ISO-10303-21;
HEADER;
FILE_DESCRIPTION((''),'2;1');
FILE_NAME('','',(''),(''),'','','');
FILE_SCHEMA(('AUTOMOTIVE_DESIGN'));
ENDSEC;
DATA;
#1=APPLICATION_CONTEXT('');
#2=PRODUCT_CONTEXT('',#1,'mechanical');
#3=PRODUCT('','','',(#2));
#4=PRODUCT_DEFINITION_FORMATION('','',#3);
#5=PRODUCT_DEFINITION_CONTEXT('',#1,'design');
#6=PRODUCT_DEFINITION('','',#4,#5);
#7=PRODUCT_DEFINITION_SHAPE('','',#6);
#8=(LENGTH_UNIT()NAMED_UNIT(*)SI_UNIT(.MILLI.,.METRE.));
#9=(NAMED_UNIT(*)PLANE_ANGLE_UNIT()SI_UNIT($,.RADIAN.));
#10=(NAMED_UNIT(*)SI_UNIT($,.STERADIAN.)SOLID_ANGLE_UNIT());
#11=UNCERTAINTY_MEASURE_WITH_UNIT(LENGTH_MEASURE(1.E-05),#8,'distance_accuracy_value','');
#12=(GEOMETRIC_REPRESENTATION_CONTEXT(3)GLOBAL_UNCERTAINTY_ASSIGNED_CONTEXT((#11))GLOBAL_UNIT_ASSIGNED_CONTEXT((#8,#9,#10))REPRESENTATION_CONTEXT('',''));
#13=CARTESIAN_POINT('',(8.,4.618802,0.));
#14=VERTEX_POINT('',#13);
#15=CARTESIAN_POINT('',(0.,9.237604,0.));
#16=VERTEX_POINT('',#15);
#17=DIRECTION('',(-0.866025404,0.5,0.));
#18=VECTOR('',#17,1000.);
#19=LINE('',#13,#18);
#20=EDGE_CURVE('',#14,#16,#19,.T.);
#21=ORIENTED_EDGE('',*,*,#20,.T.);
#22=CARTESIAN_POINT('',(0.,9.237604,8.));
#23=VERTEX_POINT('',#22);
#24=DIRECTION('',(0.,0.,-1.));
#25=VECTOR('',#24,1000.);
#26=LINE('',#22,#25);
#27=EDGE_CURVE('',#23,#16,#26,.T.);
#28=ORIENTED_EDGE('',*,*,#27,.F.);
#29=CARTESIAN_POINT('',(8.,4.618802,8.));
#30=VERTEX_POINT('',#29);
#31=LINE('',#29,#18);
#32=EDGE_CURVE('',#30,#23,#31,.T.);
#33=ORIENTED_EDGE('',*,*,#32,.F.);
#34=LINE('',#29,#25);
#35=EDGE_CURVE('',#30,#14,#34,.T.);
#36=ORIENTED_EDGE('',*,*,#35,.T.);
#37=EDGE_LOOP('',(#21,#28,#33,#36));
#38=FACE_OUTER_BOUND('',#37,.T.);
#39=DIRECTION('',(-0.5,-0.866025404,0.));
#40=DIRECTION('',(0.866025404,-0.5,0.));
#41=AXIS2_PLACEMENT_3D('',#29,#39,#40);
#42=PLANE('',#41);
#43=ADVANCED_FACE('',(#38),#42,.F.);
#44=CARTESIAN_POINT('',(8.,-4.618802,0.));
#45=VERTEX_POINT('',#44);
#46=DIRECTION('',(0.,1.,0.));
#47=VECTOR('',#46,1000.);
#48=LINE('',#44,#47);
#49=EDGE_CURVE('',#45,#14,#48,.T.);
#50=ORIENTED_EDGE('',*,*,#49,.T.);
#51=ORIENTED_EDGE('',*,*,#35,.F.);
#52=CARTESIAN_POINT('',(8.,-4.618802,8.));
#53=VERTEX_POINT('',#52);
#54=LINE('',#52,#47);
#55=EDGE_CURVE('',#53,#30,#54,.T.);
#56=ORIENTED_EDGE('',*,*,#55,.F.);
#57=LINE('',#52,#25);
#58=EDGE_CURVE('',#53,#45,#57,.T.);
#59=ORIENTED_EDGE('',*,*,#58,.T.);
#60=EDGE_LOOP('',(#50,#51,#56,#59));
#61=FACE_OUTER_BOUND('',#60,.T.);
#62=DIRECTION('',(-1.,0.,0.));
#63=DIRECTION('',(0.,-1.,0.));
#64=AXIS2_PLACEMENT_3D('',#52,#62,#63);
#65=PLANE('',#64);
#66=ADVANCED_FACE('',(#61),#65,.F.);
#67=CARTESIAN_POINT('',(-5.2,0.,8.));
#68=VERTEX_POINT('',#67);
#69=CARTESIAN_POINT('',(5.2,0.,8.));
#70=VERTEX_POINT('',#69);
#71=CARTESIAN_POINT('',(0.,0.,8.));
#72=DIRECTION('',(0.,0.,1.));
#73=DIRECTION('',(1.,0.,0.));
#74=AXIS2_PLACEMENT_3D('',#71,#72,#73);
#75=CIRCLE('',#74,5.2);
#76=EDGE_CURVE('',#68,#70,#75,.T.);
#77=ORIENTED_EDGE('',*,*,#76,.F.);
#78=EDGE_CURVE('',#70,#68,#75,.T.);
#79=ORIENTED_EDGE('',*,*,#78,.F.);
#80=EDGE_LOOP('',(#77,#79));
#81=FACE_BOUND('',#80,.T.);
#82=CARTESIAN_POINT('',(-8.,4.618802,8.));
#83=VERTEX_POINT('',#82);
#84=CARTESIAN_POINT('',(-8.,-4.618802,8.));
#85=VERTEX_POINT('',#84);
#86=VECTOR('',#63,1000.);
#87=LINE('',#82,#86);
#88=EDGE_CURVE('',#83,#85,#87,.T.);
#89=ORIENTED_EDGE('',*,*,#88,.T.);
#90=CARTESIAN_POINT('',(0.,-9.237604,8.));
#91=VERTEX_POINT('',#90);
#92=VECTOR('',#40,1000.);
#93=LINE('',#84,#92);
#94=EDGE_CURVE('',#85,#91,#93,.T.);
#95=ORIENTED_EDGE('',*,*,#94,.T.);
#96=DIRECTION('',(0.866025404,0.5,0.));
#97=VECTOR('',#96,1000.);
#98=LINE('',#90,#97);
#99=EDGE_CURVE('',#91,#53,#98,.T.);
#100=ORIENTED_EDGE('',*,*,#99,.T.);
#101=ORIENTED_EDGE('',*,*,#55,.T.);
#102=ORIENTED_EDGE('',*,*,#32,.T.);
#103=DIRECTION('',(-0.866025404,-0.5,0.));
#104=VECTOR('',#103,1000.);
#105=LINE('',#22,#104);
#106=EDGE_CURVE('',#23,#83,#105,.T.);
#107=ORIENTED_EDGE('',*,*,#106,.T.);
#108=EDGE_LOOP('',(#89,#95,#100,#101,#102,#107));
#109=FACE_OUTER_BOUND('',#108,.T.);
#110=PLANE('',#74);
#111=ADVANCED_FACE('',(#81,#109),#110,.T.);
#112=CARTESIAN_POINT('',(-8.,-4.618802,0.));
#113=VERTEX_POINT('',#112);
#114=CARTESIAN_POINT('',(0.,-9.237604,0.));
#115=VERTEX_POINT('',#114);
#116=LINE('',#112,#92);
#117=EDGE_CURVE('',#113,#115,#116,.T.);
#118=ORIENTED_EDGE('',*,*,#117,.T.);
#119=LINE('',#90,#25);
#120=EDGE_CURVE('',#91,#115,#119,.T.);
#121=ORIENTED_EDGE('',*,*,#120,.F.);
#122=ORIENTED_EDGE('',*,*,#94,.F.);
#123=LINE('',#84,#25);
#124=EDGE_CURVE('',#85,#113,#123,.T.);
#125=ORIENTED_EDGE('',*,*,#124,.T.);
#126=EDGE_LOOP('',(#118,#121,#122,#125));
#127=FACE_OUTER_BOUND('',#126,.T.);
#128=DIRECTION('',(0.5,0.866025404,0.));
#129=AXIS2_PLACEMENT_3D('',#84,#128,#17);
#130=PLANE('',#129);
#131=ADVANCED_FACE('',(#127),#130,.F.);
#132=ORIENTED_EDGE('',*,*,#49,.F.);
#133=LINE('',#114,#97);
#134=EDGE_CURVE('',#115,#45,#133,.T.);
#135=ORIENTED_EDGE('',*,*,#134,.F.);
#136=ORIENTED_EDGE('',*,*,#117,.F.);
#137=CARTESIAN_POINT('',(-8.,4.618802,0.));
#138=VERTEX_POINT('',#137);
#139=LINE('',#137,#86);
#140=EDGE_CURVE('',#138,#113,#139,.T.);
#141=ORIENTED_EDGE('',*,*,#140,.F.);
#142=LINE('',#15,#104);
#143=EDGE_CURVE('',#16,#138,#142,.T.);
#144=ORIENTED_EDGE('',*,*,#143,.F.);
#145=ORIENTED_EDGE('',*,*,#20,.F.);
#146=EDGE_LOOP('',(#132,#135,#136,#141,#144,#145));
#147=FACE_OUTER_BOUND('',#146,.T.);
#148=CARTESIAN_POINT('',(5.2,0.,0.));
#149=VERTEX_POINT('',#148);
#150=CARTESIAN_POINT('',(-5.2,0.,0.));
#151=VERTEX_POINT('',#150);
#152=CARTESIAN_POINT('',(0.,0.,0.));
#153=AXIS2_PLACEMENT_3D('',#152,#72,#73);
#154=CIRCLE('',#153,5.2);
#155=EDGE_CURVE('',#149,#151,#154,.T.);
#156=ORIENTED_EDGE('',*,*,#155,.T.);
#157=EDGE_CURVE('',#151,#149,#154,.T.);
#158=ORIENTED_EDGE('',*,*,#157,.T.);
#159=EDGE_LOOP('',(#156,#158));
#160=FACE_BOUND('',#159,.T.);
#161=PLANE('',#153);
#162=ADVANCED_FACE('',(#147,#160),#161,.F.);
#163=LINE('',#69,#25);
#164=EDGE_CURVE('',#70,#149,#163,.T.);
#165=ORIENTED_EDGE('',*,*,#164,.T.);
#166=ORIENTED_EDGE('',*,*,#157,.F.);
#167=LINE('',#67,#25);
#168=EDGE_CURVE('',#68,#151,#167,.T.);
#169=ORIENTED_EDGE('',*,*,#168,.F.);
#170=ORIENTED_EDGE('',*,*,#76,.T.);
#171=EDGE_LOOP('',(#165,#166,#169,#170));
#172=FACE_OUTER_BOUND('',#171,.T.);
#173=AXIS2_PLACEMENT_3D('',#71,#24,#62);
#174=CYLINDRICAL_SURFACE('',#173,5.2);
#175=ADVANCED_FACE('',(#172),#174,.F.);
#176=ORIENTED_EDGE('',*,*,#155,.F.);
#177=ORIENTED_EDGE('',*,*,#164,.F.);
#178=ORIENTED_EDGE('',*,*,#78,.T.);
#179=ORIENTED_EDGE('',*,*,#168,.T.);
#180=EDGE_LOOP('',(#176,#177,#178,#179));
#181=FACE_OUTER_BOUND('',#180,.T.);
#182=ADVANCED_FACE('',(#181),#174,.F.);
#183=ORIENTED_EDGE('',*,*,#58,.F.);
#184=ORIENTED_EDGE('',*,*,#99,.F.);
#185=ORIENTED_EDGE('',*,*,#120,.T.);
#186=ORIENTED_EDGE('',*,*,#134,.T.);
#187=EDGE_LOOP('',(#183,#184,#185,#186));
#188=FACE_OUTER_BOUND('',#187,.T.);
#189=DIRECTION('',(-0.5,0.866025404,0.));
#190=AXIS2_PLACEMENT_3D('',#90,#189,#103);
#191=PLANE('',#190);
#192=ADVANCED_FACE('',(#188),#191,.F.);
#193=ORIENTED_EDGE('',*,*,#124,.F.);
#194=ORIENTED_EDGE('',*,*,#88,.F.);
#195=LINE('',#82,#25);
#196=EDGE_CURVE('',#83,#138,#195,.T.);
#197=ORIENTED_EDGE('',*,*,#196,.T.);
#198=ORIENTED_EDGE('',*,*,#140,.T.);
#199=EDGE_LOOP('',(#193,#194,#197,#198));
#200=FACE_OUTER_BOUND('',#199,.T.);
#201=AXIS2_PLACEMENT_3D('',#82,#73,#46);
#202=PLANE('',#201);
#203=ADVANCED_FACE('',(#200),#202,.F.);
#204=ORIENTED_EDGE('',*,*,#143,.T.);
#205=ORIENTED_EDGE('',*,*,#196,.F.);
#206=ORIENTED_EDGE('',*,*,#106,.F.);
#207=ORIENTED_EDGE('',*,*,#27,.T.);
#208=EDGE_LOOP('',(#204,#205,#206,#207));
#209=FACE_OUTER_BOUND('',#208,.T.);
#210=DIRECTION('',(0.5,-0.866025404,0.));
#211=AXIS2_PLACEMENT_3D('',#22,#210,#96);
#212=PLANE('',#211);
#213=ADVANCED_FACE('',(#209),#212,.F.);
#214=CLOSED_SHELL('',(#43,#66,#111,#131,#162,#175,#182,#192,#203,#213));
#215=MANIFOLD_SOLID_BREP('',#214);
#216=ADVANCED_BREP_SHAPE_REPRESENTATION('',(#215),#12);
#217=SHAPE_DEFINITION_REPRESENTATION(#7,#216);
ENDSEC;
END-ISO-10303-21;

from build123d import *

# Parameters (mm, degrees)
SKETCH1_R           = 5.2
BOSS_EXTRUDE1_DEPTH = 8


with BuildPart() as part:
    # Sketch1 → Boss-Extrude1 (new body)
    with BuildSketch(Plane.XY):
        Polygon((0, 9.237604307), (-8, 4.618802154), (-8, -4.618802154), (0, -9.237604307), (8, -4.618802154), (8, 4.618802154), align=None)
        Circle(SKETCH1_R, mode=Mode.SUBTRACT)
    extrude(amount=BOSS_EXTRUDE1_DEPTH)


solid = part.part
